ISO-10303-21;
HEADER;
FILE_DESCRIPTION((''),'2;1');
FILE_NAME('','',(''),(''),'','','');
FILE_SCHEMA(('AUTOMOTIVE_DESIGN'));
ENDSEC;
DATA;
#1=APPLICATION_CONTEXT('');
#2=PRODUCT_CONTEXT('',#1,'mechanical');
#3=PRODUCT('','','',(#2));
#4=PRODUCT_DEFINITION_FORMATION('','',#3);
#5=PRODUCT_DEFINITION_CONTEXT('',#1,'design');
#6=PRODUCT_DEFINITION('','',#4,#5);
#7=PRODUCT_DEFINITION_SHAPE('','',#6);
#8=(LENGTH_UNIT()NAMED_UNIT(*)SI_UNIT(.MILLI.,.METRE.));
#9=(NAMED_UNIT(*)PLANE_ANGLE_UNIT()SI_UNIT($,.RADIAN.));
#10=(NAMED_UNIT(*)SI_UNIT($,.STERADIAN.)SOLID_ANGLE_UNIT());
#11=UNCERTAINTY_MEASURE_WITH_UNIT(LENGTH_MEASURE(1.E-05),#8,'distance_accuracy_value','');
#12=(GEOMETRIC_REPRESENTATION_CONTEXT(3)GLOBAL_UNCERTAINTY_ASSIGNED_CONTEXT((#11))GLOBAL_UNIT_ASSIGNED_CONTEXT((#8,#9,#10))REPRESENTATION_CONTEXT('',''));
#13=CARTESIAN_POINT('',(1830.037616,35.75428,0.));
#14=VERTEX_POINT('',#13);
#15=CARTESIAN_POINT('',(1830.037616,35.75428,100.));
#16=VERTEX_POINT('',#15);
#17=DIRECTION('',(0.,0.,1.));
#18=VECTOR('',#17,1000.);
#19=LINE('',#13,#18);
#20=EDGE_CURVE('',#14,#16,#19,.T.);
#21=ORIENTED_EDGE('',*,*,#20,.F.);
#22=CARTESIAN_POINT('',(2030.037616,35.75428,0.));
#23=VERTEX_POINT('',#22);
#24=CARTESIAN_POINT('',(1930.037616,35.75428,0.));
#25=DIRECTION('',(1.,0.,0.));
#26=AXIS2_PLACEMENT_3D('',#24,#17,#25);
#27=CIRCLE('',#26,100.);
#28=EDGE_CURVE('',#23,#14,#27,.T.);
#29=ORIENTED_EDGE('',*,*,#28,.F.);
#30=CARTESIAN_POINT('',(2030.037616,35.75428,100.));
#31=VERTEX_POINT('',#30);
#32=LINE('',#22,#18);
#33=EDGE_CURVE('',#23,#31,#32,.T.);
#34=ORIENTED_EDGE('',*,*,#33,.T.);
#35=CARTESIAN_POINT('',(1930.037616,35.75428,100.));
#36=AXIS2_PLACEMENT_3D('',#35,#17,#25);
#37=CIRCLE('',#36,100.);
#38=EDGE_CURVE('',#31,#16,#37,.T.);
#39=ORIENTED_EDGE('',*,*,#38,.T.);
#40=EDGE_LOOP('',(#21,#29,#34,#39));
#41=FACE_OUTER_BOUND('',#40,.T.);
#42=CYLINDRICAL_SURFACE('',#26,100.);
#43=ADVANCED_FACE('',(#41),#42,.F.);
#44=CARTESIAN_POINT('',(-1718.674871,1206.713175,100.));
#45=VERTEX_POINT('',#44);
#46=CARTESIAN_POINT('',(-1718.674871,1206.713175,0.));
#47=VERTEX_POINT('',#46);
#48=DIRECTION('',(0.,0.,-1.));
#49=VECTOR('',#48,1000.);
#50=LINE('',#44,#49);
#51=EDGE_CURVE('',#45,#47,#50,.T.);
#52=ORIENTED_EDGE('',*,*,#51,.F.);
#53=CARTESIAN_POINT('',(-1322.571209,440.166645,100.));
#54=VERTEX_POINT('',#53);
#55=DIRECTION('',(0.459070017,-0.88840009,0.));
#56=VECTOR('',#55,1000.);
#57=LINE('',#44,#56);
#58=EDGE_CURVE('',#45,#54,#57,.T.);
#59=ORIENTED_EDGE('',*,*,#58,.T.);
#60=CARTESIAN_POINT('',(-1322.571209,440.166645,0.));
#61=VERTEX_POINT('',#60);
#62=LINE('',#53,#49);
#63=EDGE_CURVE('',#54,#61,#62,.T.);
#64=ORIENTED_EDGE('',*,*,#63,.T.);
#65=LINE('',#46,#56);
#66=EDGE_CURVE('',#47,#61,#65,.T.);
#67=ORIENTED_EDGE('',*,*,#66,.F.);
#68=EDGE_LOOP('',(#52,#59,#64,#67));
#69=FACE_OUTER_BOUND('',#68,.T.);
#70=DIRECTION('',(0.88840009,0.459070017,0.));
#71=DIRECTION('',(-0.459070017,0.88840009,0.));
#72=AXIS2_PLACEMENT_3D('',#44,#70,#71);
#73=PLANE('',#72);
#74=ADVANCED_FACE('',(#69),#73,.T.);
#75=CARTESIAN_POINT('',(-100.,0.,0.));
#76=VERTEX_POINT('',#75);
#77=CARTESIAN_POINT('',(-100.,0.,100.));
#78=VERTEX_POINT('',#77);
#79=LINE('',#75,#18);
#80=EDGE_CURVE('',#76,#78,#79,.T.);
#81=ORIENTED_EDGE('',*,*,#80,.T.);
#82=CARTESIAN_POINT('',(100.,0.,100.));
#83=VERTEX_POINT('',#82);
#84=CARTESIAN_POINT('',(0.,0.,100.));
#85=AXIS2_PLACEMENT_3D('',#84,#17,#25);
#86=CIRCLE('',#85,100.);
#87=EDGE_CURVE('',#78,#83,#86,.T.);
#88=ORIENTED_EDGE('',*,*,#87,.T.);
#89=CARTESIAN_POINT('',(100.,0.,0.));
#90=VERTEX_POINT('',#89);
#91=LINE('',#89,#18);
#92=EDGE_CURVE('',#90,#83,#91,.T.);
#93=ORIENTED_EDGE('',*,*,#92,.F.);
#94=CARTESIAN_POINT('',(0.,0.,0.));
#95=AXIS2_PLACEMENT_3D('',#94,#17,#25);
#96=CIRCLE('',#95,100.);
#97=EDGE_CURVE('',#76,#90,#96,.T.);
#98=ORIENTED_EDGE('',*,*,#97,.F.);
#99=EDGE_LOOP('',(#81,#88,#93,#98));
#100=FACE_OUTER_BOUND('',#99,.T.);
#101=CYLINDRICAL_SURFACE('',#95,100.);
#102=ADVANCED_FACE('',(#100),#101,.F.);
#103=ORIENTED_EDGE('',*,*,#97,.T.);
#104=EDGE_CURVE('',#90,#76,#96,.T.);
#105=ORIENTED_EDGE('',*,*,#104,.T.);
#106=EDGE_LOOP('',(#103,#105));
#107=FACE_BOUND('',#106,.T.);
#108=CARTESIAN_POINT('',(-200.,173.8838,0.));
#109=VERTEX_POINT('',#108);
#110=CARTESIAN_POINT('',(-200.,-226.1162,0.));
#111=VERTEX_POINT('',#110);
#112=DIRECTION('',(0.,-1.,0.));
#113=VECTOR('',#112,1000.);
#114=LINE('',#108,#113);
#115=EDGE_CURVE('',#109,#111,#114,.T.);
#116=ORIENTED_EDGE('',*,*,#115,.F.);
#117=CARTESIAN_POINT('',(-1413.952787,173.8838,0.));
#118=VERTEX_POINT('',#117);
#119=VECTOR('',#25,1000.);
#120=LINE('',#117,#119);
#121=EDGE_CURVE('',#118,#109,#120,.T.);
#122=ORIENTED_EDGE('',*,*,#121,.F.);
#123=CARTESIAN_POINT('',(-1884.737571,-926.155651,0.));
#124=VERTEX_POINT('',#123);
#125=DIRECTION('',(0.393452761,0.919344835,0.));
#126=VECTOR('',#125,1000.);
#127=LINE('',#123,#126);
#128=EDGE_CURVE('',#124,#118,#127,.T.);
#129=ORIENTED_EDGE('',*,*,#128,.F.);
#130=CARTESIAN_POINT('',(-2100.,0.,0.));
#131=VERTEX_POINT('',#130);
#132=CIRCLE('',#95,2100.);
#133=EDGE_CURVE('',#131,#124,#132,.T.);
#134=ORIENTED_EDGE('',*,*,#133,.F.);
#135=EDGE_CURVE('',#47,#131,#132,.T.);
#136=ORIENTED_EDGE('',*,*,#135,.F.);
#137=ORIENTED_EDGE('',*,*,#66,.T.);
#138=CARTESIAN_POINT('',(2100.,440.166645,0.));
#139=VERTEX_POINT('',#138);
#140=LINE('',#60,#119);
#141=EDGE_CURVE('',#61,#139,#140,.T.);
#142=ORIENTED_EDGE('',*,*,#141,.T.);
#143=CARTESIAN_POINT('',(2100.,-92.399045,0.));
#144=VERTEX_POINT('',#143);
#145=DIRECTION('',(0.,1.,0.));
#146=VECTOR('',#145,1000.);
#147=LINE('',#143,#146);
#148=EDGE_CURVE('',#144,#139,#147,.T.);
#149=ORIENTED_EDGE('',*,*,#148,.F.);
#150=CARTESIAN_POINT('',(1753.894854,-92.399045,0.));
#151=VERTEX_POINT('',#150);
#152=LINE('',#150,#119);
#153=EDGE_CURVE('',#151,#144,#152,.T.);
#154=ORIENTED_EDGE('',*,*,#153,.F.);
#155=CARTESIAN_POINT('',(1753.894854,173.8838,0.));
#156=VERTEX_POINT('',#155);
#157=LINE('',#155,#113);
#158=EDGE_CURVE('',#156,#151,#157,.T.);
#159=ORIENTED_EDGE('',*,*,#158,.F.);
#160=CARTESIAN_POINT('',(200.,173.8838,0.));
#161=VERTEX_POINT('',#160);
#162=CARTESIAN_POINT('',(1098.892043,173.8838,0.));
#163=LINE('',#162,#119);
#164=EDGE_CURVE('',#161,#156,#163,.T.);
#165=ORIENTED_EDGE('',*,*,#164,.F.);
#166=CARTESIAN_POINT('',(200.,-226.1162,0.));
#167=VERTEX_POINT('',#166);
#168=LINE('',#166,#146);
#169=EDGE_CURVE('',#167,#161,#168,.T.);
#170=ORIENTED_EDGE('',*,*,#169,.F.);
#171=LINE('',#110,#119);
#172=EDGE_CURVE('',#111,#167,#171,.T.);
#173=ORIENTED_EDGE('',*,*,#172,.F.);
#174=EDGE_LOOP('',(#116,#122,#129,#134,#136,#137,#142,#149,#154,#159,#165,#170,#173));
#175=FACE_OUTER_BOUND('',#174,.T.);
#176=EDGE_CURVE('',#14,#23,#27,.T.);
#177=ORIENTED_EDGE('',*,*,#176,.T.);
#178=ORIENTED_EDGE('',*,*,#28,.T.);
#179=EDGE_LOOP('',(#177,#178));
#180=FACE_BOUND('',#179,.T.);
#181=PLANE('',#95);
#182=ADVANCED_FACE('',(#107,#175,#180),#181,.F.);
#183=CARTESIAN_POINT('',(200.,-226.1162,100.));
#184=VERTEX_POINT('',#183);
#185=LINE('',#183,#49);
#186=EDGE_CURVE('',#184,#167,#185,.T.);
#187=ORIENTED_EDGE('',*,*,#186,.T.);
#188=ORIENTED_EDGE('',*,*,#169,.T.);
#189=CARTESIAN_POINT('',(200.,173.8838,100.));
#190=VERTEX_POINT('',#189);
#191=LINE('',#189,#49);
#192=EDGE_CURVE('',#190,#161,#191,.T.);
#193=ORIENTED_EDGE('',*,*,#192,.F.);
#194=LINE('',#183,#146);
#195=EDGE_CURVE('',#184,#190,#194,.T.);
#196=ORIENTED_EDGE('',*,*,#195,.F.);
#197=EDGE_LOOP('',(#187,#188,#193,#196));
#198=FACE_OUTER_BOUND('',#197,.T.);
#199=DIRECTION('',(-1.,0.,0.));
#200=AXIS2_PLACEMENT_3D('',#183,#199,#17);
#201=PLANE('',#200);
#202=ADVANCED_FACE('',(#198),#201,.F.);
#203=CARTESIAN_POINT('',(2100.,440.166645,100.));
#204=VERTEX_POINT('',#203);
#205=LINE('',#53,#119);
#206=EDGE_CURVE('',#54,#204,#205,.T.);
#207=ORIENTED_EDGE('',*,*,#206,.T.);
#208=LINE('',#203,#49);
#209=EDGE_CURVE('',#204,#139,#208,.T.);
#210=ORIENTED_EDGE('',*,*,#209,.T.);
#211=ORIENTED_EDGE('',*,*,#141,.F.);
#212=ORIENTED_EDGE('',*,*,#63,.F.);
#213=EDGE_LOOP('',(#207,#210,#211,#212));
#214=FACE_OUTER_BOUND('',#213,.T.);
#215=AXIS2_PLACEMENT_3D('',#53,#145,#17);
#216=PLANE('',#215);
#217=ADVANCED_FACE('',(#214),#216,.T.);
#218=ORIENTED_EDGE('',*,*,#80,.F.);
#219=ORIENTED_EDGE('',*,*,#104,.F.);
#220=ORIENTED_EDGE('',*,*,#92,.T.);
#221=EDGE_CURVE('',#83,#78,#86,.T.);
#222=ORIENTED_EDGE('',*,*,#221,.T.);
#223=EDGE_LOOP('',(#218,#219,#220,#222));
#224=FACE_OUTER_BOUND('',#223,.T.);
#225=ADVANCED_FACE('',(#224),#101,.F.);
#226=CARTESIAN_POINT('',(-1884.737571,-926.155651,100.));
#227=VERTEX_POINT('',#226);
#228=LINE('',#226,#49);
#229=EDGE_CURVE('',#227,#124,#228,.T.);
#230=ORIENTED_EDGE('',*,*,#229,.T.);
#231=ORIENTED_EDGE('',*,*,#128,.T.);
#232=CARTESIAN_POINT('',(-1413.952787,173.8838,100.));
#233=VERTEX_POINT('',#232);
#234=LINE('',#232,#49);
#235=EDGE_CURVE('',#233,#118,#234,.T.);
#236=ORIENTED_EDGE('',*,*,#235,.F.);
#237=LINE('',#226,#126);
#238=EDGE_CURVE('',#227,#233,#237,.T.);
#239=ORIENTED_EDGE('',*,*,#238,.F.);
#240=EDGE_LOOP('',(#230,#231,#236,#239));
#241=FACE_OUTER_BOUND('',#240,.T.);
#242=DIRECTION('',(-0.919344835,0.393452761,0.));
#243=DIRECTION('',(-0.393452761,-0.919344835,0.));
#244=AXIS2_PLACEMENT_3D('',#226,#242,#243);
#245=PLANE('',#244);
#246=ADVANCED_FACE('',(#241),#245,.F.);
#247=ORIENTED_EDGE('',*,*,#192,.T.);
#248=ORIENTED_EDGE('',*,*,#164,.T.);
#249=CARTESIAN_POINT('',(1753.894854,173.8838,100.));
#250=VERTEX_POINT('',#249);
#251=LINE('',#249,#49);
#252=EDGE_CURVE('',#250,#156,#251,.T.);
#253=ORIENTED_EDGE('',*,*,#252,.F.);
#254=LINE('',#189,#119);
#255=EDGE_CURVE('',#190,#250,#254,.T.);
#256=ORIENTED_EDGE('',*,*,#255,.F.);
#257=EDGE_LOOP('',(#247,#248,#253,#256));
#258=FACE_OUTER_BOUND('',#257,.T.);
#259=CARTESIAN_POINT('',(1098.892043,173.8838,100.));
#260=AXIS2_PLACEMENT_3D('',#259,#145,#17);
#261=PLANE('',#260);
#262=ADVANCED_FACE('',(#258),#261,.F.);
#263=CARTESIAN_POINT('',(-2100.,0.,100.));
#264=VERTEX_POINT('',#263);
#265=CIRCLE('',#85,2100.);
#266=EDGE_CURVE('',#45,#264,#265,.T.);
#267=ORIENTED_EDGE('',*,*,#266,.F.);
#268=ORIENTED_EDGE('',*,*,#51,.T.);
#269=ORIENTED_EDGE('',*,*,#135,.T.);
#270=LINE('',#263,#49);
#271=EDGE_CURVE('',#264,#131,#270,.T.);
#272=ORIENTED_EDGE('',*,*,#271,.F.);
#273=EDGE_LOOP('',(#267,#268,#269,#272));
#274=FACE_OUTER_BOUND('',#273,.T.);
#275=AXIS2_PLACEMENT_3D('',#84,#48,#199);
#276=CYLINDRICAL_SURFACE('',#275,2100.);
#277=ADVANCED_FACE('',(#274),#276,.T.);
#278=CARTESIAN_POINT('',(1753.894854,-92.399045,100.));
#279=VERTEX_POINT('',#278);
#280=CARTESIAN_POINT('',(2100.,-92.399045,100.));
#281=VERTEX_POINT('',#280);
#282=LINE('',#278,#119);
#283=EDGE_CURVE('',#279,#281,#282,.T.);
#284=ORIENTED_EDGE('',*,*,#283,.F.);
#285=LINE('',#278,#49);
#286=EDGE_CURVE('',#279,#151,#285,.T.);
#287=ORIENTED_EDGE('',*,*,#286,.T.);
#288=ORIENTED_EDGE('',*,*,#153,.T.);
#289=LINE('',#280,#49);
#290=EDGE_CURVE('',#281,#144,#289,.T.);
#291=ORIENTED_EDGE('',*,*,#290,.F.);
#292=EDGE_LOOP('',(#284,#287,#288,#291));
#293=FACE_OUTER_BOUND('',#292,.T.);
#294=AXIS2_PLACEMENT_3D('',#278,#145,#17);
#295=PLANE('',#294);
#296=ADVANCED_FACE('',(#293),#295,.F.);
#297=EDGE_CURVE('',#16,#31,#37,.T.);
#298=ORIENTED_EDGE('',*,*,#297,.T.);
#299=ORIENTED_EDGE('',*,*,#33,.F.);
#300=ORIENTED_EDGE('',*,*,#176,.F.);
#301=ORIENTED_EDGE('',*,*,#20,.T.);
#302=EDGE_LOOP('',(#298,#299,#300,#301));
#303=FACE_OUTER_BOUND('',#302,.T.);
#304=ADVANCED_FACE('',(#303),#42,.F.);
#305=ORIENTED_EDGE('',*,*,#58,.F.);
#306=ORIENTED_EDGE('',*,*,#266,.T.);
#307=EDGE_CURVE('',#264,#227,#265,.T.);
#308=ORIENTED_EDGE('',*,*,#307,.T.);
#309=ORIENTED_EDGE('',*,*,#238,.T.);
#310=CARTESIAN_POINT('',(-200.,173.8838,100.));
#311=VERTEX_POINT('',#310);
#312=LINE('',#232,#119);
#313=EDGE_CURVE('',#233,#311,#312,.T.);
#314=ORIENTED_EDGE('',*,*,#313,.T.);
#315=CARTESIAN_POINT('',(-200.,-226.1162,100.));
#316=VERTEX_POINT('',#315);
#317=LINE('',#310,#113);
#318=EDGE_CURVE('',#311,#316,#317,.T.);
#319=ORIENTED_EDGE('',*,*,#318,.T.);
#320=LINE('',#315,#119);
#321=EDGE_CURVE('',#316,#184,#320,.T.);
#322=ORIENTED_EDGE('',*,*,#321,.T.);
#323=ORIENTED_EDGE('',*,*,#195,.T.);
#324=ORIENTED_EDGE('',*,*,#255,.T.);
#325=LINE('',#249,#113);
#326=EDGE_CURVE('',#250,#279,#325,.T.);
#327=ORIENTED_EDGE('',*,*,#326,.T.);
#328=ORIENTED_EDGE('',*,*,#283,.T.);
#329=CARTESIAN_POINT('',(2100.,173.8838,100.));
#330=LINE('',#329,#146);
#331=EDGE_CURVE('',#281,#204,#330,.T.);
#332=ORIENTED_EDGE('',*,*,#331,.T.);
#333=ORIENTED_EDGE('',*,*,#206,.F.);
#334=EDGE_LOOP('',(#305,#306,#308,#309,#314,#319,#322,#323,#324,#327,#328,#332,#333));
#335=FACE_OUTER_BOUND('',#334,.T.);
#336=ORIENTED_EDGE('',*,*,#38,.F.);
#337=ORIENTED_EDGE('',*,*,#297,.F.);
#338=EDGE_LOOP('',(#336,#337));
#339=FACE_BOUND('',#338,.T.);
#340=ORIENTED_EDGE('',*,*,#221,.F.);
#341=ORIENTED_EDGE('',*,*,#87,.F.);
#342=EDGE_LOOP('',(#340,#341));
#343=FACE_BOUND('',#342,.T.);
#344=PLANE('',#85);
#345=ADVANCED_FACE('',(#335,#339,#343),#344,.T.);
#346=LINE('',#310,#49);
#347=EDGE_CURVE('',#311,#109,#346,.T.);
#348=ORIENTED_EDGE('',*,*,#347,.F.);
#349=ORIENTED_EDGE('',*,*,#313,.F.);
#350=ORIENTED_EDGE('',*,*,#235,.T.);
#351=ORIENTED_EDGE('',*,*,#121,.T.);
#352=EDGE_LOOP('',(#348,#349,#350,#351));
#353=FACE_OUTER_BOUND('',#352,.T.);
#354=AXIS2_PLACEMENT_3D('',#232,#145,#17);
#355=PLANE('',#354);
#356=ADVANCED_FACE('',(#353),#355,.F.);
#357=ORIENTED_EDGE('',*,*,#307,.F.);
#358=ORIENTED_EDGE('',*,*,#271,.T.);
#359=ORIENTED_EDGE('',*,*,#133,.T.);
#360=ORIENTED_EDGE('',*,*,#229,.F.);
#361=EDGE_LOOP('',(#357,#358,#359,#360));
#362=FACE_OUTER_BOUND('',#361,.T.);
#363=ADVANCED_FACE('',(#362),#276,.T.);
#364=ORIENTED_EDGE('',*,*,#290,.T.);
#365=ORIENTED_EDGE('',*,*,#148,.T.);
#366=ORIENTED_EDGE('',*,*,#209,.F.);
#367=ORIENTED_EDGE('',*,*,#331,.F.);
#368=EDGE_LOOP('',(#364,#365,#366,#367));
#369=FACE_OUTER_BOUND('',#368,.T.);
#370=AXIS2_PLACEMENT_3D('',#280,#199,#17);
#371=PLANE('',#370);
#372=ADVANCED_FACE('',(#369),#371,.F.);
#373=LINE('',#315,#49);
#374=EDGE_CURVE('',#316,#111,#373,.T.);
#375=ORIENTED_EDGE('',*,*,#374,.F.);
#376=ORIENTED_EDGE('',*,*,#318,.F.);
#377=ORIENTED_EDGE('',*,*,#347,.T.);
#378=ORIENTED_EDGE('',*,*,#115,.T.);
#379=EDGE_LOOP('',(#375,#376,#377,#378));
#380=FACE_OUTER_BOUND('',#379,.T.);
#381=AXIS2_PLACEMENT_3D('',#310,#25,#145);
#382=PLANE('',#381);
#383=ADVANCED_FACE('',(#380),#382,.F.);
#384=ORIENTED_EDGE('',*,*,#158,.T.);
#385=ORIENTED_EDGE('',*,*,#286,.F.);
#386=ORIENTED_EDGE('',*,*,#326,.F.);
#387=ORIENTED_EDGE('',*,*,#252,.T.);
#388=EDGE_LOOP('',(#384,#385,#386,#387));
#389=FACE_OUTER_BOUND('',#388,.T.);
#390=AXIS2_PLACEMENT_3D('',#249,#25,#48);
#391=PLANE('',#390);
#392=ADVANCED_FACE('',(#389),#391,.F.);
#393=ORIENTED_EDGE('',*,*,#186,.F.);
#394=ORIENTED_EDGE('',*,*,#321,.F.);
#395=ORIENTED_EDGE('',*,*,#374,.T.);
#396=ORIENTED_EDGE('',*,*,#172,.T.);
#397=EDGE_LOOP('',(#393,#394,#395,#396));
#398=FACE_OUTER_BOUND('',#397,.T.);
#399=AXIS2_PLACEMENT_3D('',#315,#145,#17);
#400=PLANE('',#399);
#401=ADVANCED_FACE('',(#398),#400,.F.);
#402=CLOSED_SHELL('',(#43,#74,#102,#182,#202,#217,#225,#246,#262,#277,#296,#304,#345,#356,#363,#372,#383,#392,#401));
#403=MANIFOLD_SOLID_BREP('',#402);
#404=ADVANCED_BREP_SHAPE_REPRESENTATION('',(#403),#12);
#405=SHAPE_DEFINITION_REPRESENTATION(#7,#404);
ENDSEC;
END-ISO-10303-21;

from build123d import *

# Parameters (mm, degrees)
BOSS_EXTRUDE1_DEPTH = 100
SKETCH2_R           = 100
CUT_EXTRUDE1_DEPTH  = 100


with BuildPart() as part:
    # Sketch1 → Boss-Extrude1 (new body)
    with BuildSketch(Plane.XY):
        with BuildLine():
            Line((-1718.674871456, 1206.713174795), (-1322.571209422, 440.16664507))
            Line((-1322.571209422, 440.16664507), (2100, 440.16664507))
            Line((2100, 440.16664507), (2100, 173.883799956))
            Line((2100, 173.883799956), (2100, -92.399045159))
            Line((2100, -92.399045159), (1753.894853504, -92.399045159))
            Line((1753.894853504, -92.399045159), (1753.894853504, 173.883799956))
            Line((1753.894853504, 173.883799956), (1098.892043301, 173.883799956))
            Line((1098.892043301, 173.883799956), (200, 173.883799956))
            Line((200, 173.883799956), (200, -226.116200044))
            Line((200, -226.116200044), (-200, -226.116200044))
            Line((-200, -226.116200044), (-200, 173.883799956))
            Line((-200, 173.883799956), (-1413.952786652, 173.883799956))
            Line((-1413.952786652, 173.883799956), (-1884.737570564, -926.155651122))
            ThreePointArc((-1884.737570564, -926.155651122), (-2093.663694094, 163.010232903), (-1718.674871456, 1206.713174795))
        make_face()
    extrude(amount=BOSS_EXTRUDE1_DEPTH)

    # Sketch2 → Cut-Extrude1 (cut)
    with BuildSketch(Plane.XY.offset(100)):
        with Locations((1930.037615803, 35.754280486)):
            Circle(SKETCH2_R)
        Circle(SKETCH2_R)
    extrude(amount=-CUT_EXTRUDE1_DEPTH, mode=Mode.SUBTRACT)


solid = part.part
